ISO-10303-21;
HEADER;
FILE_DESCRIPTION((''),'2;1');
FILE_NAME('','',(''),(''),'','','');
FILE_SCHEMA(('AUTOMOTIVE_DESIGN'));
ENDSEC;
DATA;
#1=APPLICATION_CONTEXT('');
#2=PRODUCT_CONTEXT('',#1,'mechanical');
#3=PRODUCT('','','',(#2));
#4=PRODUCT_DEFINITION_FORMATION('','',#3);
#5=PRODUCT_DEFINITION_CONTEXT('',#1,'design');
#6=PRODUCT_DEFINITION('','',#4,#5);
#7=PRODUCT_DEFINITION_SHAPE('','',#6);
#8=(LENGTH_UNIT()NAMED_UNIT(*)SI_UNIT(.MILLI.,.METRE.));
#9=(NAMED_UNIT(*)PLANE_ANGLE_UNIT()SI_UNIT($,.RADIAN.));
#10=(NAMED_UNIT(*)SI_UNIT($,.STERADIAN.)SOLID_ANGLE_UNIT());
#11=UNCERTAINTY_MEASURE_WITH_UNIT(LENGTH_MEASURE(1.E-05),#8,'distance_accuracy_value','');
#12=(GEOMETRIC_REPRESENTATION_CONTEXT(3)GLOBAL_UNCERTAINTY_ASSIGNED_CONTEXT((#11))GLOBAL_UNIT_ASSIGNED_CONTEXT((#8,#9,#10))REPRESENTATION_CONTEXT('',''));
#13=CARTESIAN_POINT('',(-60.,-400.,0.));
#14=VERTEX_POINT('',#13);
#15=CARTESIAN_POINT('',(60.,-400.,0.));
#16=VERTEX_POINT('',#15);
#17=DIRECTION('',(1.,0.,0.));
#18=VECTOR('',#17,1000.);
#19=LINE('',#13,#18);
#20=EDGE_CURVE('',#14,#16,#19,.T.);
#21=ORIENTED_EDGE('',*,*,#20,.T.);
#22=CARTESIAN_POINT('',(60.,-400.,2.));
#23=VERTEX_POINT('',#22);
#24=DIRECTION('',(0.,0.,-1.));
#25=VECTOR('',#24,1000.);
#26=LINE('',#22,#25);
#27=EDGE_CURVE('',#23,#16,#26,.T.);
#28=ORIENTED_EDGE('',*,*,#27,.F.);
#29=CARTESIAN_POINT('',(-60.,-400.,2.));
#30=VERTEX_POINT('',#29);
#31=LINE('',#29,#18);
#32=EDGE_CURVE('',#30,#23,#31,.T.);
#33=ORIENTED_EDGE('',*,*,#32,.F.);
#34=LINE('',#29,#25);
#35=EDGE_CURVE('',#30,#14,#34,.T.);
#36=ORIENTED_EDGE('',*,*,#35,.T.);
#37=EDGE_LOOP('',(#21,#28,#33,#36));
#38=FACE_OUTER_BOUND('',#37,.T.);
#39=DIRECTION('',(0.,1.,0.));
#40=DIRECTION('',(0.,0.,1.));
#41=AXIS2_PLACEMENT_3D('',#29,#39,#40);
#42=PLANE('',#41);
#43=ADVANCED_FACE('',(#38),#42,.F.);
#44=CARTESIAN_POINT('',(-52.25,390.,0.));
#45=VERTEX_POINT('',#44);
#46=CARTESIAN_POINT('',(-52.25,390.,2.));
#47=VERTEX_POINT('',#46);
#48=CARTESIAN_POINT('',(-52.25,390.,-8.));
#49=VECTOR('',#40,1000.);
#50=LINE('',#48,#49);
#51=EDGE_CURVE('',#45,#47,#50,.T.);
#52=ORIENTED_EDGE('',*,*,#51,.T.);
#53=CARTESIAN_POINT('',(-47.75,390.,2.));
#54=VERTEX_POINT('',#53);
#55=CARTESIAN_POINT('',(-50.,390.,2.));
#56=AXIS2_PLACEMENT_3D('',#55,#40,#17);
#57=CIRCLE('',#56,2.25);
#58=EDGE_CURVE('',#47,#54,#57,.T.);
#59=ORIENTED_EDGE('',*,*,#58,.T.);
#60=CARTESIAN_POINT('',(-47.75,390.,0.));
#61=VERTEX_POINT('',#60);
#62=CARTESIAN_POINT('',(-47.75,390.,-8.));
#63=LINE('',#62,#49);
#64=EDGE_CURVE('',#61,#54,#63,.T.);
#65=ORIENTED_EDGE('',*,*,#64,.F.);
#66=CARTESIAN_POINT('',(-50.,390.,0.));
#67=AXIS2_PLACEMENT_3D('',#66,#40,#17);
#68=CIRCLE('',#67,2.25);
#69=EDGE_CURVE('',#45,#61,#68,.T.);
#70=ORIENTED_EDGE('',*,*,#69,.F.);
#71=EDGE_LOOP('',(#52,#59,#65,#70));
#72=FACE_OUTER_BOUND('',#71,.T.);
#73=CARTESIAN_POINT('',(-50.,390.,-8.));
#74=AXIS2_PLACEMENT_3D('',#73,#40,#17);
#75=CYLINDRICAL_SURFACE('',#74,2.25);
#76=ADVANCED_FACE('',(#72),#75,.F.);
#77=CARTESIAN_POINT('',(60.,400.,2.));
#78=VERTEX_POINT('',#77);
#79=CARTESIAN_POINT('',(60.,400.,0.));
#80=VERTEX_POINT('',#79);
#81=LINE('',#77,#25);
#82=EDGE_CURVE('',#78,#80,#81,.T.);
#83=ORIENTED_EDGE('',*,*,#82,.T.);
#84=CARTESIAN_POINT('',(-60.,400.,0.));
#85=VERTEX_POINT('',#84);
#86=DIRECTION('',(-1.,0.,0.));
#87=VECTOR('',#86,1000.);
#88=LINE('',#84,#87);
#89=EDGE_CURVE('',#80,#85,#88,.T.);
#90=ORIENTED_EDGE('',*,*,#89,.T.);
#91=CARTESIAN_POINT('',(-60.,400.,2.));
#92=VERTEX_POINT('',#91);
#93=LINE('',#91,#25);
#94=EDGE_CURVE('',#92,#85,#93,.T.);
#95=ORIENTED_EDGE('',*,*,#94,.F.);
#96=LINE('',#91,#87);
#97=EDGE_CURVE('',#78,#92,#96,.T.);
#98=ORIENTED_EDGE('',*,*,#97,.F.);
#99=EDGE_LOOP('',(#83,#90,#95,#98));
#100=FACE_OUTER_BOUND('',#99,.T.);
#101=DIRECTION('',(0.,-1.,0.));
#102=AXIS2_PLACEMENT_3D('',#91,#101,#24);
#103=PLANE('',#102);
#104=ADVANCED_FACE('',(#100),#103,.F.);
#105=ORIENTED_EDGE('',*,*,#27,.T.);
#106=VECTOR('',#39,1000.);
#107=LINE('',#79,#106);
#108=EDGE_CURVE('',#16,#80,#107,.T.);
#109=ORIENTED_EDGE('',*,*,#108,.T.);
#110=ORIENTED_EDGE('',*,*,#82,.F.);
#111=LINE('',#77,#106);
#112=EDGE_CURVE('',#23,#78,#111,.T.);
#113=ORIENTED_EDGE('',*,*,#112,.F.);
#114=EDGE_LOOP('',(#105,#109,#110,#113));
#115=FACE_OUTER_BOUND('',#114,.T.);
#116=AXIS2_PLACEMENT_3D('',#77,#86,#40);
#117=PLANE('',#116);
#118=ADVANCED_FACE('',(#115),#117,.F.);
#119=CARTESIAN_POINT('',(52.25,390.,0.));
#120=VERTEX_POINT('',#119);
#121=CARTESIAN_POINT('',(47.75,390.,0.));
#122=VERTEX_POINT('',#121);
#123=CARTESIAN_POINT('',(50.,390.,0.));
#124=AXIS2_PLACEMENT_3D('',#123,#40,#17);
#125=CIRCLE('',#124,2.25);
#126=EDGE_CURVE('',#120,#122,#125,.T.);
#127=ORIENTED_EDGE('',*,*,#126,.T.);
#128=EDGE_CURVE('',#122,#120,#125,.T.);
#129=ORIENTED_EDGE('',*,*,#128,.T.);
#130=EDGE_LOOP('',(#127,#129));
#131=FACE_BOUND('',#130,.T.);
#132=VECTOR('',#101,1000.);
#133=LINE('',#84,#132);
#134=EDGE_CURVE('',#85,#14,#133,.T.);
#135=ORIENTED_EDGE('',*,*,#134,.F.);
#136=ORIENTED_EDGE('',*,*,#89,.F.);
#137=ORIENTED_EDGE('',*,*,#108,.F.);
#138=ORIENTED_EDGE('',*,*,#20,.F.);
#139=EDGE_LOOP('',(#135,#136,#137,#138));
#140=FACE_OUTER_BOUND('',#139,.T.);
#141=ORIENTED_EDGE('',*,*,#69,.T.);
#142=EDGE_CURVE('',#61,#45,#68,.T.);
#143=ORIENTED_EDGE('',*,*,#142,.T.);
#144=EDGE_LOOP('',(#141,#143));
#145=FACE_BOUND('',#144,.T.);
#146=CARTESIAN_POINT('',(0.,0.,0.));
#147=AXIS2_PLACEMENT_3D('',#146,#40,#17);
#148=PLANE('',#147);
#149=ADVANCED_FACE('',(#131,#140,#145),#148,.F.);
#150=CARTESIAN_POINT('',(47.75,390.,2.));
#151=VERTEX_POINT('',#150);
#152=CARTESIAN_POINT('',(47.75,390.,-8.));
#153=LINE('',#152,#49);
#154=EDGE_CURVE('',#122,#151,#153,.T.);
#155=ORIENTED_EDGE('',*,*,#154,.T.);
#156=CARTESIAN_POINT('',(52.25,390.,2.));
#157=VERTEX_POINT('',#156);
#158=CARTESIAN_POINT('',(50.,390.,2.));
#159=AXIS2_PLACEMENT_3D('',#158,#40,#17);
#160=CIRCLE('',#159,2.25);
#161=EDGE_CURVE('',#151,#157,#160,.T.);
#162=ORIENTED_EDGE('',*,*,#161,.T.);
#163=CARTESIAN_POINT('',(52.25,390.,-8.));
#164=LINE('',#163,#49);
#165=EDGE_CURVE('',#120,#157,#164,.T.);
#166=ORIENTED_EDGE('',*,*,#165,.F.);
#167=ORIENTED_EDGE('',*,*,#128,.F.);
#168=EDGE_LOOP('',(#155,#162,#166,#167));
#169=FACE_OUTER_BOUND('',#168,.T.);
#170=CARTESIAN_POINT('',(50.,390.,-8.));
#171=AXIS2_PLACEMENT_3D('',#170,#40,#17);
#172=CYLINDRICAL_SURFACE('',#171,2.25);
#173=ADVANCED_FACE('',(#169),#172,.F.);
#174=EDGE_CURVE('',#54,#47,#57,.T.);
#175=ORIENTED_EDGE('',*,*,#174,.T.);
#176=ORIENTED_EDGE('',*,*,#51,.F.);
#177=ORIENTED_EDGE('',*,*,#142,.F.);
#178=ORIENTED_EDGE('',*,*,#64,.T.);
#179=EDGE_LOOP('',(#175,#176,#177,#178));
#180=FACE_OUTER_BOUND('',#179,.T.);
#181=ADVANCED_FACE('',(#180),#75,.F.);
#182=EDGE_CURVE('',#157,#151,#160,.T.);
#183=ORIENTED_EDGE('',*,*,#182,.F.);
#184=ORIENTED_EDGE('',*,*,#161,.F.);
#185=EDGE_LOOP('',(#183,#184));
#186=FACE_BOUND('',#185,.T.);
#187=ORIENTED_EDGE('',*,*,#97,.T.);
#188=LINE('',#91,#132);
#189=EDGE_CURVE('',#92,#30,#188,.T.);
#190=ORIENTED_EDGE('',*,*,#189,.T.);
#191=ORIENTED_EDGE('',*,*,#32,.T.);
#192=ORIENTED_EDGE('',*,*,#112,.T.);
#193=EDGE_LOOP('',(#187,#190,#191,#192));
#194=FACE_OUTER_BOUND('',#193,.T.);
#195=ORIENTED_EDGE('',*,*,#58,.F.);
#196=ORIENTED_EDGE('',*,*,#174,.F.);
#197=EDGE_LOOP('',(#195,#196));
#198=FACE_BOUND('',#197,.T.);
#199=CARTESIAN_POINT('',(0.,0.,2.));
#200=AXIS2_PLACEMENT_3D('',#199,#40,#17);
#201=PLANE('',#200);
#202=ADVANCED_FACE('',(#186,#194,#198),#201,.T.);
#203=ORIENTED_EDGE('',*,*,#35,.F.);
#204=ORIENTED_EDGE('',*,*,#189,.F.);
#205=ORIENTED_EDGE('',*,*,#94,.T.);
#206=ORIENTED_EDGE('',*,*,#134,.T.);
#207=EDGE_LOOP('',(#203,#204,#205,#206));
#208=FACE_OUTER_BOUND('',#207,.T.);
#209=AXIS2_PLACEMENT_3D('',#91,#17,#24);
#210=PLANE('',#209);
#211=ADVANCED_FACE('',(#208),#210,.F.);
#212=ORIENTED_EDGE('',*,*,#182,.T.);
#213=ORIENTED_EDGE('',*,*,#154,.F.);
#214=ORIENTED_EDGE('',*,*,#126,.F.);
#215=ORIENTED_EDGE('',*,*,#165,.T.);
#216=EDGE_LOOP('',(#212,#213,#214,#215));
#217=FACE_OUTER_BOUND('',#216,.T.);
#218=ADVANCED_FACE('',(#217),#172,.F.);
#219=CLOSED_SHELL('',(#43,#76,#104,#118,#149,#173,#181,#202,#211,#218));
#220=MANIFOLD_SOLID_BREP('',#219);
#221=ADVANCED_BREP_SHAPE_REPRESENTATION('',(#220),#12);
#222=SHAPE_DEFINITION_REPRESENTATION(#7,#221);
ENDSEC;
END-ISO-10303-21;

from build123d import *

# Parameters (mm, degrees)
SKETCH_1_W          = 120
SKETCH_1_H          = 800
EXTRUDE_1_DEPTH     = 2
SKETCH_2_R          = 2.25
CUT_EXTRUDE_1_DEPTH = 10


with BuildPart() as part:
    # 草图1 → 凸台-拉伸1 (new body)
    with BuildSketch(Plane.XY):
        Rectangle(SKETCH_1_W, SKETCH_1_H)
    extrude(amount=EXTRUDE_1_DEPTH)

    # 草图2 → 切除-拉伸1 (cut)
    with BuildSketch(Plane.XY.offset(2)):
        with Locations((-50, 390)):
            Circle(SKETCH_2_R)
        with Locations((50, 390)):
            Circle(SKETCH_2_R)
    extrude(amount=-CUT_EXTRUDE_1_DEPTH, mode=Mode.SUBTRACT)


solid = part.part
